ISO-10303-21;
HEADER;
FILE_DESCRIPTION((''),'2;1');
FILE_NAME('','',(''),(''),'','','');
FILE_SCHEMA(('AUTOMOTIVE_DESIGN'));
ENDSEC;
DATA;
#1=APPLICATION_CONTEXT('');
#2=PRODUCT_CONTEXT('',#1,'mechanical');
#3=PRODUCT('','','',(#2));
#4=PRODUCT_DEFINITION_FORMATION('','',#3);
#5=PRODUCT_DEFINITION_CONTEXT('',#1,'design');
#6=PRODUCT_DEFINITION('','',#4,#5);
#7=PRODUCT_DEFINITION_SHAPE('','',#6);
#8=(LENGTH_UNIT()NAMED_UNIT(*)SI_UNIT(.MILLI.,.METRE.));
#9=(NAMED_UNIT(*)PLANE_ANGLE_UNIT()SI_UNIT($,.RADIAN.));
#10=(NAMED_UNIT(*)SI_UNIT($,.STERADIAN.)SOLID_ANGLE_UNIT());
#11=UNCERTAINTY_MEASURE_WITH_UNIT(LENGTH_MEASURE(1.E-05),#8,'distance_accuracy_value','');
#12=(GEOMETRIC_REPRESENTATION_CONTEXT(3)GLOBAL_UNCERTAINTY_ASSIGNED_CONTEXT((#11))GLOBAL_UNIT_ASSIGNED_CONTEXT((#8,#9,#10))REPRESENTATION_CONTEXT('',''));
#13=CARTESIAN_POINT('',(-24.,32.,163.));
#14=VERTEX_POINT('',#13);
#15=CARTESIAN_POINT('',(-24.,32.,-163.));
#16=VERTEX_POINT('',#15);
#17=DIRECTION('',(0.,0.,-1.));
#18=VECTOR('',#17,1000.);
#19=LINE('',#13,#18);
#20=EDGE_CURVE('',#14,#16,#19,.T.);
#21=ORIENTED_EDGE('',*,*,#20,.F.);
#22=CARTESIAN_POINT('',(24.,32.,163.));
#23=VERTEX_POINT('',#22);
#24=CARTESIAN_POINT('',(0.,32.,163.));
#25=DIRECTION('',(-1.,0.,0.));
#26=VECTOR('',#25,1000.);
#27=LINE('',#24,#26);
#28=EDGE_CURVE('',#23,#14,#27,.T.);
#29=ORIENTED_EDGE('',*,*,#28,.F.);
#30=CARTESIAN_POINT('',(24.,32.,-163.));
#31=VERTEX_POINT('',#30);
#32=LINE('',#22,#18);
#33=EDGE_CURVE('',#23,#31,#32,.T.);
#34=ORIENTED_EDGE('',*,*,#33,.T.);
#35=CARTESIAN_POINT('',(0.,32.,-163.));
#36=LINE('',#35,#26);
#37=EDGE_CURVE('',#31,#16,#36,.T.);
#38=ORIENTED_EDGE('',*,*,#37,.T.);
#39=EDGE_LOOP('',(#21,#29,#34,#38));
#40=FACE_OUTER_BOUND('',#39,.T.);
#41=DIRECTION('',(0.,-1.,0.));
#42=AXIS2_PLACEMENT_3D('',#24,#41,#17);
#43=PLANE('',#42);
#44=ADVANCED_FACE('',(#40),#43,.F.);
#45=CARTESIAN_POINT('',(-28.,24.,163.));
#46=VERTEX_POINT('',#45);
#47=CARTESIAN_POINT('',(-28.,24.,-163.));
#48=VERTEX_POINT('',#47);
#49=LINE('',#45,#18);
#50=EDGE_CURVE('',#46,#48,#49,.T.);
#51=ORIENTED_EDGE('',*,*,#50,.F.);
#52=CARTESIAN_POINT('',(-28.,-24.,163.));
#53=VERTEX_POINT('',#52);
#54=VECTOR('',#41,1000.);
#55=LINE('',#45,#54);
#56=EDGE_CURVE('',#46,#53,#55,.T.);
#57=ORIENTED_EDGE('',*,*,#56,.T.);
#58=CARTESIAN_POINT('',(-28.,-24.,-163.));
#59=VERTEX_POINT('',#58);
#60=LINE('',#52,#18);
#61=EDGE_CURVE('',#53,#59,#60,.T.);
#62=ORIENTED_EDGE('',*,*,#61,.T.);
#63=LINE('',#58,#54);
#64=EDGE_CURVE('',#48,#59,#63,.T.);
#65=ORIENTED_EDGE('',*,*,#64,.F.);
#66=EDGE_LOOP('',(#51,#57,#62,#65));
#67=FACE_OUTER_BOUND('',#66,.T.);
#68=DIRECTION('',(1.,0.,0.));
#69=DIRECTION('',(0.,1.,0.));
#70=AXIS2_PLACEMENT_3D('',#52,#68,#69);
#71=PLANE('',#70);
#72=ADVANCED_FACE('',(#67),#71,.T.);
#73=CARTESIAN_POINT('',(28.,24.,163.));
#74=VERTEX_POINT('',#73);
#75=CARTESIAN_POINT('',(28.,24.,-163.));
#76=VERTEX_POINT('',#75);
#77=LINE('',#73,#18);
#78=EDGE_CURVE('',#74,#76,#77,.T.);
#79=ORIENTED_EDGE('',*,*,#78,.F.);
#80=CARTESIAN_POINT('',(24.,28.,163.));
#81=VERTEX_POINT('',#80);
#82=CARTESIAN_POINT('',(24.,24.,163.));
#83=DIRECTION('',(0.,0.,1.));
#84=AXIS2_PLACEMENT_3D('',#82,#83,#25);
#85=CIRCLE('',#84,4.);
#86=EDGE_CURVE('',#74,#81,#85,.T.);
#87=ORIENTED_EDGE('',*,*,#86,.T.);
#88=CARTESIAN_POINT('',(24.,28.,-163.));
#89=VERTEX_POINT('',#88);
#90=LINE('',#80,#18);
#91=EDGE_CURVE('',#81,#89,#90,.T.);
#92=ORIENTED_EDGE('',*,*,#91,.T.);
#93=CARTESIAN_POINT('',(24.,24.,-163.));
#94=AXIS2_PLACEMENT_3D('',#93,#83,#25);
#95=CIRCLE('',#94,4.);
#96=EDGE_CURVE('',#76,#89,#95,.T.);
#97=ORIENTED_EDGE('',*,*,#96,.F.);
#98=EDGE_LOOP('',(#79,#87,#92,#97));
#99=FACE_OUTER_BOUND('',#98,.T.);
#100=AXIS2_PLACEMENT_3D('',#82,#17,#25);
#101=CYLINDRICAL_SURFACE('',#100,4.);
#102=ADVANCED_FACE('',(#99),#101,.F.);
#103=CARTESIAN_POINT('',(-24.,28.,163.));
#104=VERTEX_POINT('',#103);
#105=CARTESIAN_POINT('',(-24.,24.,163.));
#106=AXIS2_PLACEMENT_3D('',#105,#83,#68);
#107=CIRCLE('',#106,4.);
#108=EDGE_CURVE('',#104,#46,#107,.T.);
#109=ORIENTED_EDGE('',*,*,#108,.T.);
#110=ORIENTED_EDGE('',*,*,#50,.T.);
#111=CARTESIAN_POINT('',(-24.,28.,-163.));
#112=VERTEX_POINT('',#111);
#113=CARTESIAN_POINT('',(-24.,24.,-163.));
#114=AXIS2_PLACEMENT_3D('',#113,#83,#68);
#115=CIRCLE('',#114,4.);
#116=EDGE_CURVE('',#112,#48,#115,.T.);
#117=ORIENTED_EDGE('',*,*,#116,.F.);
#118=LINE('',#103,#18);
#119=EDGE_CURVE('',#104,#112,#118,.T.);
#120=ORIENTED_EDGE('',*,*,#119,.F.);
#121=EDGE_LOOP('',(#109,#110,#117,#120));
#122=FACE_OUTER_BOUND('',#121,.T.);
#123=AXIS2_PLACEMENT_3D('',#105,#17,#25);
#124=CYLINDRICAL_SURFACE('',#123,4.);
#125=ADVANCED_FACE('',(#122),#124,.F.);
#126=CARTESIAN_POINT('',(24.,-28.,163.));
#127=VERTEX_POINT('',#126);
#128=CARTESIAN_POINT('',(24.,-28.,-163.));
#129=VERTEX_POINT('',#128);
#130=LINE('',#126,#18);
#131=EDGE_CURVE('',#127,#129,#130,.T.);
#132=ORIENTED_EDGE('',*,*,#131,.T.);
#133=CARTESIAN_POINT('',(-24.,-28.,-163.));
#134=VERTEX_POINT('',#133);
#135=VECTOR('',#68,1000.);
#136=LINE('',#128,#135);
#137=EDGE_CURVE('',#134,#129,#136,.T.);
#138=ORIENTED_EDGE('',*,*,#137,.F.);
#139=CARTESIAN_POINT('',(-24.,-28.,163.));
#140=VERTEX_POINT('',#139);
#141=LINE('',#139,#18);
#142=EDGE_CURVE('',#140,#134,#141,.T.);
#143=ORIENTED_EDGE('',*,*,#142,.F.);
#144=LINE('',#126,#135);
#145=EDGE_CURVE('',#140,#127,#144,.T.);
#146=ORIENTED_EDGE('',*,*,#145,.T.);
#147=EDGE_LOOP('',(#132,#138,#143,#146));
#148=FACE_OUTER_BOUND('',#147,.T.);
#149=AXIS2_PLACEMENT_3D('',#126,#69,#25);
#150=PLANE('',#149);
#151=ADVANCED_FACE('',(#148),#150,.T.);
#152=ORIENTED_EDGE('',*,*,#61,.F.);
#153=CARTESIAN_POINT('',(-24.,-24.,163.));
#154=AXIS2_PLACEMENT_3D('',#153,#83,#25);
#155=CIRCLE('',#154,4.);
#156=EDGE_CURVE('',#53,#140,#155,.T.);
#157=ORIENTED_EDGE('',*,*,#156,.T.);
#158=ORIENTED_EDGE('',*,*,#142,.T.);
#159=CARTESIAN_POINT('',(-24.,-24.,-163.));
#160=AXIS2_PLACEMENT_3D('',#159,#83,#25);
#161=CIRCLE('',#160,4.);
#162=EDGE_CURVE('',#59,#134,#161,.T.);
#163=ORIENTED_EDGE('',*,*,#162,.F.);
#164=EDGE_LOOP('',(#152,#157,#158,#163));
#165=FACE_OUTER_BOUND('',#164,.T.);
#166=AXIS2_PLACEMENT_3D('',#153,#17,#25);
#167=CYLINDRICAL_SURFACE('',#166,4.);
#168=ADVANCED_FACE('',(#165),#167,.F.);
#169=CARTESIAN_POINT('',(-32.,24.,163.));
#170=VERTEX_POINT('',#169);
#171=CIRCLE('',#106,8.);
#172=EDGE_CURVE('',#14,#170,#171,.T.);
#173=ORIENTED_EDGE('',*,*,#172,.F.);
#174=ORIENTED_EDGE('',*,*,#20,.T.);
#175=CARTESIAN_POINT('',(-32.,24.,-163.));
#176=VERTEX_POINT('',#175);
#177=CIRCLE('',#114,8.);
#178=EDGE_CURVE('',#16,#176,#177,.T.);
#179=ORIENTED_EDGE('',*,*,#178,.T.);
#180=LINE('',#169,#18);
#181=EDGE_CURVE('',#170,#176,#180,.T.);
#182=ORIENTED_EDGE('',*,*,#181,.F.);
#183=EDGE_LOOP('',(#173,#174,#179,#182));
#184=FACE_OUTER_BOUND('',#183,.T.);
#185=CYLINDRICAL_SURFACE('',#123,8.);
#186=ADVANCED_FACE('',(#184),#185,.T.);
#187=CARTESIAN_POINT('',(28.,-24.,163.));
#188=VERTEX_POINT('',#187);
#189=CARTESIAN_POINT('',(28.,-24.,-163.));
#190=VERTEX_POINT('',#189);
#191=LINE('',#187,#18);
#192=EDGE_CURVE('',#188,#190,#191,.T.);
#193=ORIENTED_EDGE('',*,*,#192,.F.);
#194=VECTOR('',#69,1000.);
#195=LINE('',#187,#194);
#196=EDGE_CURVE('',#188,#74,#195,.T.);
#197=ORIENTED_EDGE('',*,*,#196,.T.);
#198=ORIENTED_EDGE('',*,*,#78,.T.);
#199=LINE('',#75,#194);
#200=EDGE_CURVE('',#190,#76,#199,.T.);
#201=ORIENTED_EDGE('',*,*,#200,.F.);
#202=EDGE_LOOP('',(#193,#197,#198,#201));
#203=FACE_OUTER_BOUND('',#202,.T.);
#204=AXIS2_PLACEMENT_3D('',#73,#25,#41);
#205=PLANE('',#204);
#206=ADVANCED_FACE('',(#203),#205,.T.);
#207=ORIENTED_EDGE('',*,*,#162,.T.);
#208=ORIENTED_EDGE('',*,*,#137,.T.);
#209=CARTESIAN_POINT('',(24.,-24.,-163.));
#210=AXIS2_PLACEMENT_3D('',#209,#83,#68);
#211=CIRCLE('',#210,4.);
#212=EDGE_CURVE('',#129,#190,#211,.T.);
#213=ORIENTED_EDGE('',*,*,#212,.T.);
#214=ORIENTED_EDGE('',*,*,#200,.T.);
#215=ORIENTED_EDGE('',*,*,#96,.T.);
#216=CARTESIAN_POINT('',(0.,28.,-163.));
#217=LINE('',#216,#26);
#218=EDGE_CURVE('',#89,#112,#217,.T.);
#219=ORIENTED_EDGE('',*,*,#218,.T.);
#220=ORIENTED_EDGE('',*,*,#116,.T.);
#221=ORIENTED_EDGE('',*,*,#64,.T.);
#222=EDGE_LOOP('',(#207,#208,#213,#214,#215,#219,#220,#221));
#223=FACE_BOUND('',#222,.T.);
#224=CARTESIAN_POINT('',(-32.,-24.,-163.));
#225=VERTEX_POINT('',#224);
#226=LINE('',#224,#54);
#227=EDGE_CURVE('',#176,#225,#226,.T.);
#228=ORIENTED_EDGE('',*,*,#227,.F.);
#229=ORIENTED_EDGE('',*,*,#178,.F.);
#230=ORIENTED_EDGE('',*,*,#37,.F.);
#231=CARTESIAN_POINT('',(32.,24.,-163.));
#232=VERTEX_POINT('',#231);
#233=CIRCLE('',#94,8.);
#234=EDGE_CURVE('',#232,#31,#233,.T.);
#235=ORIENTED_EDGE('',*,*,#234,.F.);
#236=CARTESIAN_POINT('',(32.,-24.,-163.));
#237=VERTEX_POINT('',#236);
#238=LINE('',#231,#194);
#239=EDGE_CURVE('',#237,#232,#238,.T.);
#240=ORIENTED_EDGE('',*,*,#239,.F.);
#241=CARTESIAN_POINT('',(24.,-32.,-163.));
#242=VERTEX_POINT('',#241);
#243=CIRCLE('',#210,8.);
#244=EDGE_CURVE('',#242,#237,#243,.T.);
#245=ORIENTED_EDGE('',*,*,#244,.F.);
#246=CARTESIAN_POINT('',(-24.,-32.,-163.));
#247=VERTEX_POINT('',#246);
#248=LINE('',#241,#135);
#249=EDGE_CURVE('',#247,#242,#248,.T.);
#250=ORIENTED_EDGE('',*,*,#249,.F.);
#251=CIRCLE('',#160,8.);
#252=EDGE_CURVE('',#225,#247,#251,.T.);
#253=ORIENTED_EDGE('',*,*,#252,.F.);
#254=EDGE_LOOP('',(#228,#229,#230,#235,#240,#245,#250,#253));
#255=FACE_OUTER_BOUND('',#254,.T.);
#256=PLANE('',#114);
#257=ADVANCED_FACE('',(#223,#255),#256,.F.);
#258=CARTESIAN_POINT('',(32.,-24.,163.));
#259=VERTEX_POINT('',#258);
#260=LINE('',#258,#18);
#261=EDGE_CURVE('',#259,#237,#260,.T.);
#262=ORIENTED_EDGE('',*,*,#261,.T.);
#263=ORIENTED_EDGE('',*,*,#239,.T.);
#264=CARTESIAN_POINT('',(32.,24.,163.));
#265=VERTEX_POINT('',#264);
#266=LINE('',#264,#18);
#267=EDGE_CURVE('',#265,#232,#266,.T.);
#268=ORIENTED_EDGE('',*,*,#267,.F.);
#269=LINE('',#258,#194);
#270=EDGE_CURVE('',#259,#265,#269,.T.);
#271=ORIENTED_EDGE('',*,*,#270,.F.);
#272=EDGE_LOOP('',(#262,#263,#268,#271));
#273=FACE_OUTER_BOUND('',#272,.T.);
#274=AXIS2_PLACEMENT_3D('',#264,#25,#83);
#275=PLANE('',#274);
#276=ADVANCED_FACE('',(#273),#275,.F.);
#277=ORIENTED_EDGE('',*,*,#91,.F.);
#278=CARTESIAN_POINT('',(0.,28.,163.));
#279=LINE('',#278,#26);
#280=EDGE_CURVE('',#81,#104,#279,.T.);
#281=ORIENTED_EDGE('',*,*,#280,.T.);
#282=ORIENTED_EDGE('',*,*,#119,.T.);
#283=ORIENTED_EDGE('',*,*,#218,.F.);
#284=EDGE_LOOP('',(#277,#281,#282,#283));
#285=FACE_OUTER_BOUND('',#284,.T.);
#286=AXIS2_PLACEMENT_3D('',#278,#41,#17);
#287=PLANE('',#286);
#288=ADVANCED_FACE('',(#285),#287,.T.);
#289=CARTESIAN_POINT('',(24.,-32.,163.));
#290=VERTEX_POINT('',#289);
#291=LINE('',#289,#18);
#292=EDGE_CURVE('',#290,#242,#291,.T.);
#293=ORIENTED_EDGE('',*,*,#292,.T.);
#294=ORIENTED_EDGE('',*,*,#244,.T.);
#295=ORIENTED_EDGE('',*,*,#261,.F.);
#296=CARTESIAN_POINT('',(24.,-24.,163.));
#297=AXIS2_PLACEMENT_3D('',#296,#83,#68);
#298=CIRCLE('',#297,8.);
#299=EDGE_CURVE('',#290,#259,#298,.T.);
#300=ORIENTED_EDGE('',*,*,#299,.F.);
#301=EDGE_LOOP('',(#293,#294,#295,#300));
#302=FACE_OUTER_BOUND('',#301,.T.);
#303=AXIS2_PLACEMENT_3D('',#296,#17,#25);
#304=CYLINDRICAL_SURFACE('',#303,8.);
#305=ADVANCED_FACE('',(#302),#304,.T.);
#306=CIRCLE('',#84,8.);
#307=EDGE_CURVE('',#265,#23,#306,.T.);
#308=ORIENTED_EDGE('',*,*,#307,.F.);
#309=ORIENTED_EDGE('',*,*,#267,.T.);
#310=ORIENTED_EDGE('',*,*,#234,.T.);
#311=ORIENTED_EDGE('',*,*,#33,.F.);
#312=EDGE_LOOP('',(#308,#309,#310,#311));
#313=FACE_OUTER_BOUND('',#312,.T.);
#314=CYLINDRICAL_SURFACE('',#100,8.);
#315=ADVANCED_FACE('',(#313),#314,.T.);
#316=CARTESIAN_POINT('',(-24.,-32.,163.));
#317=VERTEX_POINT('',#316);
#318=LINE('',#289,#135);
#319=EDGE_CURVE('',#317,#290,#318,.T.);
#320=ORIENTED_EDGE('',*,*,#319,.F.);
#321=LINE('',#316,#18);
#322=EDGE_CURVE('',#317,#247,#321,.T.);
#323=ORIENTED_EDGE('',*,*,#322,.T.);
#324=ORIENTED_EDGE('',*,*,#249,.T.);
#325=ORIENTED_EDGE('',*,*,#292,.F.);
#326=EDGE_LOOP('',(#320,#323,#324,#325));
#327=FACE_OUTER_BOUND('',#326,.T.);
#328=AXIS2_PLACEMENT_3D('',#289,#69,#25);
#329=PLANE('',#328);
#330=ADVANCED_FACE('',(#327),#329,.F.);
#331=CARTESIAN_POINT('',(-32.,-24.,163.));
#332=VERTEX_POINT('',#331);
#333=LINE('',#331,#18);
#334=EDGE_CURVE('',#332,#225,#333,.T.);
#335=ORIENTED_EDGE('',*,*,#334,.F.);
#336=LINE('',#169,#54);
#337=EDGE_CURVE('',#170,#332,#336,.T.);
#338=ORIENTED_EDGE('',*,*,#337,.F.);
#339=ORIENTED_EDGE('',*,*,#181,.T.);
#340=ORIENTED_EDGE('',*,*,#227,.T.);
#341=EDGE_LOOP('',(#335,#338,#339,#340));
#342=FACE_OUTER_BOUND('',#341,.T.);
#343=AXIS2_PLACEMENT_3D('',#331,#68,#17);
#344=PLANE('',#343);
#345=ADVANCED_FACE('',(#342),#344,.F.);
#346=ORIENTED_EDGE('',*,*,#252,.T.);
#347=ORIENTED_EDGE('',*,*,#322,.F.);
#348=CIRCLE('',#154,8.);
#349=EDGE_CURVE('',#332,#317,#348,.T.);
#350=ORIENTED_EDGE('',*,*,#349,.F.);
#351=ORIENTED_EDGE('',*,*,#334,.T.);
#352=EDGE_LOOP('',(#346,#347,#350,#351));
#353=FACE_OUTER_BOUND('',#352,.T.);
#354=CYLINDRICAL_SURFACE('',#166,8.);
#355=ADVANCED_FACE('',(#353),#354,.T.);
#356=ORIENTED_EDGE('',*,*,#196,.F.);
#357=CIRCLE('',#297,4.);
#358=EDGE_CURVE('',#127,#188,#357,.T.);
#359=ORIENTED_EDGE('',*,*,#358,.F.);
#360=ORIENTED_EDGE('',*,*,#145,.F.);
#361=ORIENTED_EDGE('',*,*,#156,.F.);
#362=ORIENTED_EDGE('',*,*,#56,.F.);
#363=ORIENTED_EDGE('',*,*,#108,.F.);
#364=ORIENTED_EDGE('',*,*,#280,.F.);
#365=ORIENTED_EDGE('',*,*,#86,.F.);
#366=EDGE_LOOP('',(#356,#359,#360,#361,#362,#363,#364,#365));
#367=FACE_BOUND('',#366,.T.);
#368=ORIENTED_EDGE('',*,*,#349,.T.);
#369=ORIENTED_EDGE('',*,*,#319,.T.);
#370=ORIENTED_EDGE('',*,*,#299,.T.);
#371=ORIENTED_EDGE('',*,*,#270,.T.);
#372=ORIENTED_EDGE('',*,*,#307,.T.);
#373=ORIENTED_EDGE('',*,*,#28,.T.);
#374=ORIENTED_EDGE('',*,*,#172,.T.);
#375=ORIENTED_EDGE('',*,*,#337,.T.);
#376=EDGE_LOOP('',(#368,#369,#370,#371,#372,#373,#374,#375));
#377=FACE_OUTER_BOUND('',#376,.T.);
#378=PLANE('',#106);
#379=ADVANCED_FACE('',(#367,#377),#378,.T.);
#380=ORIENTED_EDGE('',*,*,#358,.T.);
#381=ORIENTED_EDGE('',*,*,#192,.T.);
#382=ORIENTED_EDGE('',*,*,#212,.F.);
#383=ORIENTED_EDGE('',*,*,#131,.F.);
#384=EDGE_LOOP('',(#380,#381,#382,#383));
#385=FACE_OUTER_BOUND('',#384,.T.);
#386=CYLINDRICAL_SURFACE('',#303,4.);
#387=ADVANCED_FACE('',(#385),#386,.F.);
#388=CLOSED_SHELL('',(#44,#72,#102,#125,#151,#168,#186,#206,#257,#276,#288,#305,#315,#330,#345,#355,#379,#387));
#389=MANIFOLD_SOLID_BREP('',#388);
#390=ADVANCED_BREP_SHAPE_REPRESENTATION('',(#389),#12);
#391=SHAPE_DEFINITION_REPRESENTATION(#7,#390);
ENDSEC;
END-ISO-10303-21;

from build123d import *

# Parameters (mm, degrees)
BOSS_EXTRUDE_1_DEPTH = 163


with BuildPart() as part:
    # Sketch 1 → Boss-Extrude 1 (new, symmetric)
    with BuildSketch(Plane.XY):
        with BuildLine():
            Line((0, 32), (-24, 32))
            ThreePointArc((-24, 32), (-29.656854249, 29.656854249), (-32, 24))
            Line((-32, 24), (-32, 0))
            Line((-32, 0), (-32, -24))
            ThreePointArc((-32, -24), (-29.656854249, -29.656854249), (-24, -32))
            Line((-24, -32), (24, -32))
            ThreePointArc((24, -32), (29.656854249, -29.656854249), (32, -24))
            Line((32, -24), (32, 0))
            Line((32, 0), (32, 24))
            ThreePointArc((32, 24), (29.656854249, 29.656854249), (24, 32))
            Line((24, 32), (0, 32))
        make_face()
        with BuildLine():
            Line((0, 28), (-24, 28))
            ThreePointArc((-24, 28), (-26.828427125, 26.828427125), (-28, 24))
            Line((-28, 24), (-28, 0))
            Line((-28, 0), (-28, -24))
            ThreePointArc((-28, -24), (-26.828427125, -26.828427125), (-24, -28))
            Line((-24, -28), (24, -28))
            ThreePointArc((24, -28), (26.828427125, -26.828427125), (28, -24))
            Line((28, -24), (28, 0))
            Line((28, 0), (28, 24))
            ThreePointArc((28, 24), (26.828427125, 26.828427125), (24, 28))
            Line((24, 28), (0, 28))
        make_face(mode=Mode.SUBTRACT)
    extrude(amount=BOSS_EXTRUDE_1_DEPTH, both=True)


solid = part.part
